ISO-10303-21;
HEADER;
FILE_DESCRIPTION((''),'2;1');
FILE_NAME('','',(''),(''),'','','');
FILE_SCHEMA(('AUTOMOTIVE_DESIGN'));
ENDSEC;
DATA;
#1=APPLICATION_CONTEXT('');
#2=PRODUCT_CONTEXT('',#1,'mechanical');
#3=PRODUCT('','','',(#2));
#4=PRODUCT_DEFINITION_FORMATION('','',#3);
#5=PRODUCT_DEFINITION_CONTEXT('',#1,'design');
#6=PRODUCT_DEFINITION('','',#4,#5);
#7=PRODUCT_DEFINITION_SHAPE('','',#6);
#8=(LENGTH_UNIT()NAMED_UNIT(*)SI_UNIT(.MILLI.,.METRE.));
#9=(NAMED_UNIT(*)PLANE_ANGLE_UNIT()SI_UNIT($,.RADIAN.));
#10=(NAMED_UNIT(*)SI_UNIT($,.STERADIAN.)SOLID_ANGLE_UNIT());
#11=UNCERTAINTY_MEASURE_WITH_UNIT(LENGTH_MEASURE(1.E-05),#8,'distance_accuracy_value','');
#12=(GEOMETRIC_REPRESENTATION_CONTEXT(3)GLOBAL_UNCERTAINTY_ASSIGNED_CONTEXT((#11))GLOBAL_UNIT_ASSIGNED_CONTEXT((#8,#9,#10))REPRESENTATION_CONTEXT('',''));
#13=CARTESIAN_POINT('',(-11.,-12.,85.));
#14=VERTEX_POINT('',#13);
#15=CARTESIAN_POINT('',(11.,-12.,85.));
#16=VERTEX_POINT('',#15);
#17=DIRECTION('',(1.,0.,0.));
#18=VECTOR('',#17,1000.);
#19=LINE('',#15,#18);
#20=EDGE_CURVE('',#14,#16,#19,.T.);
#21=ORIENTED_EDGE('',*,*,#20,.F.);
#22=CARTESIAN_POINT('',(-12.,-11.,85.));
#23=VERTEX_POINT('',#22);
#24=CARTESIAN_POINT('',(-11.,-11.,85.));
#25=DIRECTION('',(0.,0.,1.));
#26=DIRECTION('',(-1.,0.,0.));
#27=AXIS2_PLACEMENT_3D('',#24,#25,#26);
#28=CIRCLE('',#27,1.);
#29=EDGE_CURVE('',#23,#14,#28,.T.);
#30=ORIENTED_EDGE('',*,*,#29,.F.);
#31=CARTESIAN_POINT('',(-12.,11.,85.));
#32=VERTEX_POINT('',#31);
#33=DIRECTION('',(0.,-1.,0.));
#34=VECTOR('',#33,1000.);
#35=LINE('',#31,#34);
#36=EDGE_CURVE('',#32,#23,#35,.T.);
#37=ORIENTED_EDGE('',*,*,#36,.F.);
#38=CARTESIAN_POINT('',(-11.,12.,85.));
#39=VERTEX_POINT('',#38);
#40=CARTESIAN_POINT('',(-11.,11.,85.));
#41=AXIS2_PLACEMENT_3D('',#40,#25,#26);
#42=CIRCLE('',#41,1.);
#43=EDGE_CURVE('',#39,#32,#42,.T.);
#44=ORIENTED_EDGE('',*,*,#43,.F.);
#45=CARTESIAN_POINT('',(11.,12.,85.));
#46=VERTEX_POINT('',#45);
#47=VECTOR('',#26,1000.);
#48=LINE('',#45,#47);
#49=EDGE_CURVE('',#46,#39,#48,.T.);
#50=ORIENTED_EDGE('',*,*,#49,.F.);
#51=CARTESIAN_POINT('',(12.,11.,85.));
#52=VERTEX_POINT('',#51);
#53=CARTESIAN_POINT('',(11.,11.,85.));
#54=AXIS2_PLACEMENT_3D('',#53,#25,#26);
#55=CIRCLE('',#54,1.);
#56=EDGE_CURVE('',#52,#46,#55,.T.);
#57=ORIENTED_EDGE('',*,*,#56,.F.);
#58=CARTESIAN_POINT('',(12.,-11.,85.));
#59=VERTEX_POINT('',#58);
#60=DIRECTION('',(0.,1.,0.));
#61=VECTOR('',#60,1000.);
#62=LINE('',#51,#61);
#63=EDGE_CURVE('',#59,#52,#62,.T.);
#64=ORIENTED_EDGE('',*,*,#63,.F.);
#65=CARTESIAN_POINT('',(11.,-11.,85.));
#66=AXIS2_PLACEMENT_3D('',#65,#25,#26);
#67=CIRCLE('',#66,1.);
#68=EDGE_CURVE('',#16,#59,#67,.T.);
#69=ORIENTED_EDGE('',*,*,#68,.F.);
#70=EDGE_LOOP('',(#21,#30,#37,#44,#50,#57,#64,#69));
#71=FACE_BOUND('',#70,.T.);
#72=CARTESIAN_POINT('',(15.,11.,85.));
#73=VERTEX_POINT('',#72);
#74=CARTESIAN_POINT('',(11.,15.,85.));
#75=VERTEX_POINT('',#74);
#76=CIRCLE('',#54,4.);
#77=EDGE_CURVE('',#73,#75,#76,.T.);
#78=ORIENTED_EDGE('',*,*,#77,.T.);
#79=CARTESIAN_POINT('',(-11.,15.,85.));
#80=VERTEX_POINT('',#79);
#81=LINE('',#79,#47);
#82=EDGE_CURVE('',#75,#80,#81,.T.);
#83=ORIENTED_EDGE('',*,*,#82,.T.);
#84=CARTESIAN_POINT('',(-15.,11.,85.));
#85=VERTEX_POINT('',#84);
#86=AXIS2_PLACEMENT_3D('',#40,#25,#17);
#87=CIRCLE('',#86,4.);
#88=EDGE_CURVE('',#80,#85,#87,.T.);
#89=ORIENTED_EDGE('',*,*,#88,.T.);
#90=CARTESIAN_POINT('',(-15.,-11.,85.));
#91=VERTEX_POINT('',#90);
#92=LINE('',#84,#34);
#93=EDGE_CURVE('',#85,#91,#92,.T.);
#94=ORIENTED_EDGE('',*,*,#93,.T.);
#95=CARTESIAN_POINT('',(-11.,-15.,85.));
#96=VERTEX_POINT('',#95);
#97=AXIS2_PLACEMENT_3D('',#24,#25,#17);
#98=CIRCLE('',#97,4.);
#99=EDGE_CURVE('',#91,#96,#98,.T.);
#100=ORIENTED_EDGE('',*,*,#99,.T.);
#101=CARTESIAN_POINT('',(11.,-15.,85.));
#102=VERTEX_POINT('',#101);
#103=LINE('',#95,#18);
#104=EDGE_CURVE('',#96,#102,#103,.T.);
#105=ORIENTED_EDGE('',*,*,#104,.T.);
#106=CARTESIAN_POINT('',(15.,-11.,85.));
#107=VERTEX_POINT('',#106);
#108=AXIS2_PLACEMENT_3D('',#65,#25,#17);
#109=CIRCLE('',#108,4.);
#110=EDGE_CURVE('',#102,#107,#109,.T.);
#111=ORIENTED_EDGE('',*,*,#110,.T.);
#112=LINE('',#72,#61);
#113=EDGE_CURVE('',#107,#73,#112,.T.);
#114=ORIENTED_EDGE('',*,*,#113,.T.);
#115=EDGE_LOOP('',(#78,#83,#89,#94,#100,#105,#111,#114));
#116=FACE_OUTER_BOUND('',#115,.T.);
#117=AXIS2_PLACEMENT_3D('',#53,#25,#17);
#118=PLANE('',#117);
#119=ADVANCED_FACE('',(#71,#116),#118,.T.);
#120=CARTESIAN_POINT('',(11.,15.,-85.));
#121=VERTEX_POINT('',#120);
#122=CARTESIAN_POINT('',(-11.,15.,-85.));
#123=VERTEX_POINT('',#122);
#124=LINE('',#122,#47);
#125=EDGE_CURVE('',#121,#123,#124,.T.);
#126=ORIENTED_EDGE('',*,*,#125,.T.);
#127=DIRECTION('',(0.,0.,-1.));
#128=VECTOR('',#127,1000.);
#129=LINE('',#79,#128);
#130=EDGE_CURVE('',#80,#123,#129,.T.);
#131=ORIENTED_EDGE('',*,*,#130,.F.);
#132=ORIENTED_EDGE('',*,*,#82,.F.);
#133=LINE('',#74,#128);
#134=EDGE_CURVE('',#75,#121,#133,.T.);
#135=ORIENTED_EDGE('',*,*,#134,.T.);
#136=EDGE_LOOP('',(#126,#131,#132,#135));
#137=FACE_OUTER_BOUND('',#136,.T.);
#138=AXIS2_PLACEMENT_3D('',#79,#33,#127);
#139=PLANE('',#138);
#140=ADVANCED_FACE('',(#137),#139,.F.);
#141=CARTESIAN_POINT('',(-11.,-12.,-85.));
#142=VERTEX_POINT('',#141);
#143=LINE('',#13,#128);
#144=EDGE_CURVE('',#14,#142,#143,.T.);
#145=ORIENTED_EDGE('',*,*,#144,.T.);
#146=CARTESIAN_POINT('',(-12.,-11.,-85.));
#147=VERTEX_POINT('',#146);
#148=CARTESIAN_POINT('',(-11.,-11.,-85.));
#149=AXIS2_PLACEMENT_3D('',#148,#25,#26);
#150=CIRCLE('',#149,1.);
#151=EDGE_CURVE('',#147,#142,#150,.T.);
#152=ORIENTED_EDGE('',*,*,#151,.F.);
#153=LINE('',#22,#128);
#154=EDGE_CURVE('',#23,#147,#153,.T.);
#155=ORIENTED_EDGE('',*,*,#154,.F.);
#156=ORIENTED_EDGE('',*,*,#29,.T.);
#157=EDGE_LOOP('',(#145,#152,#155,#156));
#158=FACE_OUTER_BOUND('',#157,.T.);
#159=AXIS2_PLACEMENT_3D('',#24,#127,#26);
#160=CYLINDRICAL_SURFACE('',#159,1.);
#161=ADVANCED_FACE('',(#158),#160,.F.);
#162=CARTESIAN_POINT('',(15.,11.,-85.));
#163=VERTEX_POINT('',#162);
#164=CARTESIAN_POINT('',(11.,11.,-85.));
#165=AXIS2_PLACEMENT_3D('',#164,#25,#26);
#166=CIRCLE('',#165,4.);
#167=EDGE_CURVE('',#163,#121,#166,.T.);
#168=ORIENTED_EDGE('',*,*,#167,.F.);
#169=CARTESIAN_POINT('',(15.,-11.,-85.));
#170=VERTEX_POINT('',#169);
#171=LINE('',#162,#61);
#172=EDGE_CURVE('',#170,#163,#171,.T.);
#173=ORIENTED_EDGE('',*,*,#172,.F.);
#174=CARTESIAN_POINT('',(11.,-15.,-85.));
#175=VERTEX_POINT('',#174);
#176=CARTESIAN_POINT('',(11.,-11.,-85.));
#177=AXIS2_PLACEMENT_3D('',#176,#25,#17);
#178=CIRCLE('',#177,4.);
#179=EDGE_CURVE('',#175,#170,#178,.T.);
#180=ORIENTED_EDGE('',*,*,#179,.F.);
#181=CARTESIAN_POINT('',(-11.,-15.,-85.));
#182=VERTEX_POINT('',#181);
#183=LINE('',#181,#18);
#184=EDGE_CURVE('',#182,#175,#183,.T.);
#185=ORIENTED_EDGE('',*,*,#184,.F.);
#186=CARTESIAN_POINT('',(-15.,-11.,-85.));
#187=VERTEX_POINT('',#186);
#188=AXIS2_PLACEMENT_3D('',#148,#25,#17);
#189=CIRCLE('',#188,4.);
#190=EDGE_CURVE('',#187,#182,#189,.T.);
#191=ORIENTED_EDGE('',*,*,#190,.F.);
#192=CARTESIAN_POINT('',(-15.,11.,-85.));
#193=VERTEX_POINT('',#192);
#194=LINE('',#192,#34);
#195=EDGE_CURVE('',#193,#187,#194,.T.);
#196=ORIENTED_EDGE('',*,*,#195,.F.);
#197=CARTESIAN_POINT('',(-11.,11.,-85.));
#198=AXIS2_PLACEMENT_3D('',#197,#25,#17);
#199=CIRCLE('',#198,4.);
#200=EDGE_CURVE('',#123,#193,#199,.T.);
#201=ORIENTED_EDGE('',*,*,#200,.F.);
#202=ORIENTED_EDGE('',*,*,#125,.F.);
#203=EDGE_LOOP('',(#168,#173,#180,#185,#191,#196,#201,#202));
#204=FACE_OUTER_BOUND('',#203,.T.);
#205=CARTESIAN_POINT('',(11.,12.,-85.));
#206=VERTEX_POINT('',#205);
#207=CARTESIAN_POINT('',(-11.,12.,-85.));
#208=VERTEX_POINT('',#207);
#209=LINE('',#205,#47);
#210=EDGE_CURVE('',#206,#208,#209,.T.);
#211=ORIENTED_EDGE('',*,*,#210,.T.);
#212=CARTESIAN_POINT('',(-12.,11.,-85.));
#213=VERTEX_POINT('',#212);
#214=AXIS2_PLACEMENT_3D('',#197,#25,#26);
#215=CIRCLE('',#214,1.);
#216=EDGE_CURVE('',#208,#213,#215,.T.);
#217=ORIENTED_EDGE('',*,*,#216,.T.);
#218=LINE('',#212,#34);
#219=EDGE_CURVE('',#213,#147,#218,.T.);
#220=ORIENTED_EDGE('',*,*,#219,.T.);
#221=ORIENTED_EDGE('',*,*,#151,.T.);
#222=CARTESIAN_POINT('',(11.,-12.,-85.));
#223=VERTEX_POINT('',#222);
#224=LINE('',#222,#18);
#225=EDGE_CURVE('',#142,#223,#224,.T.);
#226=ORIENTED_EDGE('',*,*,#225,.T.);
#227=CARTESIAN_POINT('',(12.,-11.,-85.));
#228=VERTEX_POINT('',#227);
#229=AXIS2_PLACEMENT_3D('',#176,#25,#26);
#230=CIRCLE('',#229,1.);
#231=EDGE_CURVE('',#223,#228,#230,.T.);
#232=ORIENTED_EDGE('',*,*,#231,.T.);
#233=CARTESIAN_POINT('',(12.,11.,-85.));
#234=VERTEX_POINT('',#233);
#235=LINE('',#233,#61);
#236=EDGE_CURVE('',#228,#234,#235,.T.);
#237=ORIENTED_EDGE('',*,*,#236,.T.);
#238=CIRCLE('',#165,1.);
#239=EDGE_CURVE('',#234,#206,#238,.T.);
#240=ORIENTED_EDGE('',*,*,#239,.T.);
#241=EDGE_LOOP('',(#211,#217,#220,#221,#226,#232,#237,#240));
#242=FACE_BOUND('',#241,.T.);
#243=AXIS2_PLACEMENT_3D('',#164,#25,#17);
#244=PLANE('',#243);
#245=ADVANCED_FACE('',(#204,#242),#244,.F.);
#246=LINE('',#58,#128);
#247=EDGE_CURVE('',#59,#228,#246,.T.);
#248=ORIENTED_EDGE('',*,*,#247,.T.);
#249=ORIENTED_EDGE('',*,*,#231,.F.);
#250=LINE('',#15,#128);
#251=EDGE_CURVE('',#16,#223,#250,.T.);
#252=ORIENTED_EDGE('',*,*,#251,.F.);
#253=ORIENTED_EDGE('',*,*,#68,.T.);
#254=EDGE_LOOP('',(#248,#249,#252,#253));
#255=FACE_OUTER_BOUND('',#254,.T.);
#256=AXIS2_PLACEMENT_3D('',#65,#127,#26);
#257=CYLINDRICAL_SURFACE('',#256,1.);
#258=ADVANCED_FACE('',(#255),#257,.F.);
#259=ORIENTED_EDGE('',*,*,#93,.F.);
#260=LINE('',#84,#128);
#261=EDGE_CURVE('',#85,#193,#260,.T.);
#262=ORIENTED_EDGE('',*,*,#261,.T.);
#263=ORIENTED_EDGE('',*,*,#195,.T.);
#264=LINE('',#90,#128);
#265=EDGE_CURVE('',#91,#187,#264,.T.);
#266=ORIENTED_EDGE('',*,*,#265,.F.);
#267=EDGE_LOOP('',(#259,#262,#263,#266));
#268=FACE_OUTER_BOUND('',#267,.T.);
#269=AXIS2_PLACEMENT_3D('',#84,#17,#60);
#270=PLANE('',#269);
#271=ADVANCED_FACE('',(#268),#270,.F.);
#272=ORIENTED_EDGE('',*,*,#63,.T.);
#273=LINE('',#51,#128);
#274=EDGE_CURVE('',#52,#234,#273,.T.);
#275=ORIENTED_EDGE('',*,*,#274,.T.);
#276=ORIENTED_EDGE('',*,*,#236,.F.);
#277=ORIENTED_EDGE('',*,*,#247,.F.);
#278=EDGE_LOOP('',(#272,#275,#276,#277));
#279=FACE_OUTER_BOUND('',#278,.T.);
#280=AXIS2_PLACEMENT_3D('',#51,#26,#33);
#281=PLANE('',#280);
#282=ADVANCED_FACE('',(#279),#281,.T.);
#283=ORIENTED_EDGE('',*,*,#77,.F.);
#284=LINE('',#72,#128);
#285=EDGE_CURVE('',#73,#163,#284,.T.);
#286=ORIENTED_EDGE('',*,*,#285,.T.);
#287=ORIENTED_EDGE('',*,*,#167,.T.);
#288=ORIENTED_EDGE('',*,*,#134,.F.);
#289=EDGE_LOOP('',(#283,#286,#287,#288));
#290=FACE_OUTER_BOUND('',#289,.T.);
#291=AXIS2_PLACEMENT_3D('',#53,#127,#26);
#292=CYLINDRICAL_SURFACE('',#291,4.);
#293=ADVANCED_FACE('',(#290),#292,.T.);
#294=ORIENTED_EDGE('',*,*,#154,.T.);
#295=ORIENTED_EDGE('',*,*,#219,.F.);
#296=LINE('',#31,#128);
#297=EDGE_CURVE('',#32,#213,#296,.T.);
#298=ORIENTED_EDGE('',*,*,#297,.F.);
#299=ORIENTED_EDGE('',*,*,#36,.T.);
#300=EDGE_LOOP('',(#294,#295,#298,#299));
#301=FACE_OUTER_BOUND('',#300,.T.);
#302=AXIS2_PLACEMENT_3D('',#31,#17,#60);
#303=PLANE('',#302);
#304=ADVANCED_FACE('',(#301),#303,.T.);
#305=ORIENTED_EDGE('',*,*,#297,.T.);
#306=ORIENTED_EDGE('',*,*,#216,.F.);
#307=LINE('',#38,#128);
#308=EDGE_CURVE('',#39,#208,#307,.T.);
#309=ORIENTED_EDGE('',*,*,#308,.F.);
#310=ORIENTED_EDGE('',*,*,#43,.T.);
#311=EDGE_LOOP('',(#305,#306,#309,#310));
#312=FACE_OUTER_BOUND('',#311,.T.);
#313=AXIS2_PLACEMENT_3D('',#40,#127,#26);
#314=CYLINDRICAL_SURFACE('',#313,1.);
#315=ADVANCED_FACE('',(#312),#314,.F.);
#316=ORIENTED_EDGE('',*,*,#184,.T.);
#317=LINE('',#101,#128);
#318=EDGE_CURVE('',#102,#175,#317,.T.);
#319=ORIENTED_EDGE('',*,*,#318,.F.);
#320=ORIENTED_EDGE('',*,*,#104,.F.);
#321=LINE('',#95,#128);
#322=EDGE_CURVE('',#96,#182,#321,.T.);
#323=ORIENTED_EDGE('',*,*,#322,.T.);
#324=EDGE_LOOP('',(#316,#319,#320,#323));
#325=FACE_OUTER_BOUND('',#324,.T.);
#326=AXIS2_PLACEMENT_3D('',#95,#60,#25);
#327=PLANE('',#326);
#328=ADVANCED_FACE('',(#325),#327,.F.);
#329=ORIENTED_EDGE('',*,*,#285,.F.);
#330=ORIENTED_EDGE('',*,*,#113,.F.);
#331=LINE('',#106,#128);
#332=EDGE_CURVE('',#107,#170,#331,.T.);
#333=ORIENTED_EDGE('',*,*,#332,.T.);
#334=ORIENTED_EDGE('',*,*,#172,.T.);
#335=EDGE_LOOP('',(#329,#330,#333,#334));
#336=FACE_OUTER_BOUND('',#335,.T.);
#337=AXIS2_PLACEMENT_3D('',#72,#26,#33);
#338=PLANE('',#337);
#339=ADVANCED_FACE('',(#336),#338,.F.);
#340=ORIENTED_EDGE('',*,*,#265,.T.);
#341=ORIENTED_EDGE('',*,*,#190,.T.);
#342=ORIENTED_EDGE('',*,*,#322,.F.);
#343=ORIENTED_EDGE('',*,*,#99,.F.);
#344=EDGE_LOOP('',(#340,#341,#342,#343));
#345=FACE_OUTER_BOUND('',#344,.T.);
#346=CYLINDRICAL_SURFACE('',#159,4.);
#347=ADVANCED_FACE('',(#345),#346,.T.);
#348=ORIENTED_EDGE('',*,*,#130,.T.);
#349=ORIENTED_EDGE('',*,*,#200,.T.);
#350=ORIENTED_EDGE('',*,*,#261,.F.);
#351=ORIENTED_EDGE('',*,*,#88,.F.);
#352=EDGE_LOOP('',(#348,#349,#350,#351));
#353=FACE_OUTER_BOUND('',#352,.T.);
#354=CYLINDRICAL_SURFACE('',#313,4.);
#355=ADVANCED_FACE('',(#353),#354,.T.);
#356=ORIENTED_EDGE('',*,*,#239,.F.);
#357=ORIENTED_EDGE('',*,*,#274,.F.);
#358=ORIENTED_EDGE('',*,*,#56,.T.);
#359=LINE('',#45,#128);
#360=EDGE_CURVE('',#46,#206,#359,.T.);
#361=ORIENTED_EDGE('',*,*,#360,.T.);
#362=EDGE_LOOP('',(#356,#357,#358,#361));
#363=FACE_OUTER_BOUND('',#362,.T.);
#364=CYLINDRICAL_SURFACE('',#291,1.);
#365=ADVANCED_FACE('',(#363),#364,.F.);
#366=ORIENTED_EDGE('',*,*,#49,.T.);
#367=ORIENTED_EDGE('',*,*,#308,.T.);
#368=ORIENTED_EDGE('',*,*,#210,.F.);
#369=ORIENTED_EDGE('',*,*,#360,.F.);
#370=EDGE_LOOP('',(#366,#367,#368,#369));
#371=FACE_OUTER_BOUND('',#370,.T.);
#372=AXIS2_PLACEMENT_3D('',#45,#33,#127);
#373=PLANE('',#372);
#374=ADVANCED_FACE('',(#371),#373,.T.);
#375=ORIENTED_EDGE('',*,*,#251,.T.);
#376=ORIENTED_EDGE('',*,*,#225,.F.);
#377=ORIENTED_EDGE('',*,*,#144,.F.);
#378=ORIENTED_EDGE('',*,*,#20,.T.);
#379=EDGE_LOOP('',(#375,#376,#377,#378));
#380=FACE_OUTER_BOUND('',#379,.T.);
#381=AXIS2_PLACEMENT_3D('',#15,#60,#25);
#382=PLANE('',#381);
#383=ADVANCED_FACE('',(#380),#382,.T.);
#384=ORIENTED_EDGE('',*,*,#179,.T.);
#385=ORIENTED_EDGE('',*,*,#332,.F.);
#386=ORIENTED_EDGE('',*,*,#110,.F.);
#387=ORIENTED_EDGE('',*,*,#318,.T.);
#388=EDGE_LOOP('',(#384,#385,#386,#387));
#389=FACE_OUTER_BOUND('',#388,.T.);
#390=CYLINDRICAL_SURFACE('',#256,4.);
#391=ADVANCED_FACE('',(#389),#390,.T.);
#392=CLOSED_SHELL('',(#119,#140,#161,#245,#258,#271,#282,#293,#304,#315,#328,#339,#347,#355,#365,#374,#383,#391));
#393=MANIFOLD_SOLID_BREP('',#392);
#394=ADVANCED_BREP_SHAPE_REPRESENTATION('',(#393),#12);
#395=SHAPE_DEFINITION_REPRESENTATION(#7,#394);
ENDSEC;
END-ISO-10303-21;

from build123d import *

# Parameters (mm, degrees)
EXTRUDE_1_DEPTH = 85


with BuildPart() as part:
    # 草图2 → 拉伸-薄壁1 (new, symmetric)
    with BuildSketch(Plane.XY):
        with BuildLine():
            Line((-11, 15), (11, 15))
            ThreePointArc((11, 15), (13.828427125, 13.828427125), (15, 11))
            Line((15, 11), (15, -11))
            ThreePointArc((15, -11), (13.828427125, -13.828427125), (11, -15))
            Line((11, -15), (-11, -15))
            ThreePointArc((-11, -15), (-13.828427125, -13.828427125), (-15, -11))
            Line((-15, -11), (-15, 11))
            ThreePointArc((-15, 11), (-13.828427125, 13.828427125), (-11, 15))
        make_face()
        with BuildLine():
            Line((-11, 12), (11, 12))
            ThreePointArc((11, 12), (11.707106781, 11.707106781), (12, 11))
            Line((12, 11), (12, -11))
            ThreePointArc((12, -11), (11.707106781, -11.707106781), (11, -12))
            Line((11, -12), (-11, -12))
            ThreePointArc((-11, -12), (-11.707106781, -11.707106781), (-12, -11))
            Line((-12, -11), (-12, 11))
            ThreePointArc((-12, 11), (-11.707106781, 11.707106781), (-11, 12))
        make_face(mode=Mode.SUBTRACT)
    extrude(amount=EXTRUDE_1_DEPTH, both=True)


solid = part.part
